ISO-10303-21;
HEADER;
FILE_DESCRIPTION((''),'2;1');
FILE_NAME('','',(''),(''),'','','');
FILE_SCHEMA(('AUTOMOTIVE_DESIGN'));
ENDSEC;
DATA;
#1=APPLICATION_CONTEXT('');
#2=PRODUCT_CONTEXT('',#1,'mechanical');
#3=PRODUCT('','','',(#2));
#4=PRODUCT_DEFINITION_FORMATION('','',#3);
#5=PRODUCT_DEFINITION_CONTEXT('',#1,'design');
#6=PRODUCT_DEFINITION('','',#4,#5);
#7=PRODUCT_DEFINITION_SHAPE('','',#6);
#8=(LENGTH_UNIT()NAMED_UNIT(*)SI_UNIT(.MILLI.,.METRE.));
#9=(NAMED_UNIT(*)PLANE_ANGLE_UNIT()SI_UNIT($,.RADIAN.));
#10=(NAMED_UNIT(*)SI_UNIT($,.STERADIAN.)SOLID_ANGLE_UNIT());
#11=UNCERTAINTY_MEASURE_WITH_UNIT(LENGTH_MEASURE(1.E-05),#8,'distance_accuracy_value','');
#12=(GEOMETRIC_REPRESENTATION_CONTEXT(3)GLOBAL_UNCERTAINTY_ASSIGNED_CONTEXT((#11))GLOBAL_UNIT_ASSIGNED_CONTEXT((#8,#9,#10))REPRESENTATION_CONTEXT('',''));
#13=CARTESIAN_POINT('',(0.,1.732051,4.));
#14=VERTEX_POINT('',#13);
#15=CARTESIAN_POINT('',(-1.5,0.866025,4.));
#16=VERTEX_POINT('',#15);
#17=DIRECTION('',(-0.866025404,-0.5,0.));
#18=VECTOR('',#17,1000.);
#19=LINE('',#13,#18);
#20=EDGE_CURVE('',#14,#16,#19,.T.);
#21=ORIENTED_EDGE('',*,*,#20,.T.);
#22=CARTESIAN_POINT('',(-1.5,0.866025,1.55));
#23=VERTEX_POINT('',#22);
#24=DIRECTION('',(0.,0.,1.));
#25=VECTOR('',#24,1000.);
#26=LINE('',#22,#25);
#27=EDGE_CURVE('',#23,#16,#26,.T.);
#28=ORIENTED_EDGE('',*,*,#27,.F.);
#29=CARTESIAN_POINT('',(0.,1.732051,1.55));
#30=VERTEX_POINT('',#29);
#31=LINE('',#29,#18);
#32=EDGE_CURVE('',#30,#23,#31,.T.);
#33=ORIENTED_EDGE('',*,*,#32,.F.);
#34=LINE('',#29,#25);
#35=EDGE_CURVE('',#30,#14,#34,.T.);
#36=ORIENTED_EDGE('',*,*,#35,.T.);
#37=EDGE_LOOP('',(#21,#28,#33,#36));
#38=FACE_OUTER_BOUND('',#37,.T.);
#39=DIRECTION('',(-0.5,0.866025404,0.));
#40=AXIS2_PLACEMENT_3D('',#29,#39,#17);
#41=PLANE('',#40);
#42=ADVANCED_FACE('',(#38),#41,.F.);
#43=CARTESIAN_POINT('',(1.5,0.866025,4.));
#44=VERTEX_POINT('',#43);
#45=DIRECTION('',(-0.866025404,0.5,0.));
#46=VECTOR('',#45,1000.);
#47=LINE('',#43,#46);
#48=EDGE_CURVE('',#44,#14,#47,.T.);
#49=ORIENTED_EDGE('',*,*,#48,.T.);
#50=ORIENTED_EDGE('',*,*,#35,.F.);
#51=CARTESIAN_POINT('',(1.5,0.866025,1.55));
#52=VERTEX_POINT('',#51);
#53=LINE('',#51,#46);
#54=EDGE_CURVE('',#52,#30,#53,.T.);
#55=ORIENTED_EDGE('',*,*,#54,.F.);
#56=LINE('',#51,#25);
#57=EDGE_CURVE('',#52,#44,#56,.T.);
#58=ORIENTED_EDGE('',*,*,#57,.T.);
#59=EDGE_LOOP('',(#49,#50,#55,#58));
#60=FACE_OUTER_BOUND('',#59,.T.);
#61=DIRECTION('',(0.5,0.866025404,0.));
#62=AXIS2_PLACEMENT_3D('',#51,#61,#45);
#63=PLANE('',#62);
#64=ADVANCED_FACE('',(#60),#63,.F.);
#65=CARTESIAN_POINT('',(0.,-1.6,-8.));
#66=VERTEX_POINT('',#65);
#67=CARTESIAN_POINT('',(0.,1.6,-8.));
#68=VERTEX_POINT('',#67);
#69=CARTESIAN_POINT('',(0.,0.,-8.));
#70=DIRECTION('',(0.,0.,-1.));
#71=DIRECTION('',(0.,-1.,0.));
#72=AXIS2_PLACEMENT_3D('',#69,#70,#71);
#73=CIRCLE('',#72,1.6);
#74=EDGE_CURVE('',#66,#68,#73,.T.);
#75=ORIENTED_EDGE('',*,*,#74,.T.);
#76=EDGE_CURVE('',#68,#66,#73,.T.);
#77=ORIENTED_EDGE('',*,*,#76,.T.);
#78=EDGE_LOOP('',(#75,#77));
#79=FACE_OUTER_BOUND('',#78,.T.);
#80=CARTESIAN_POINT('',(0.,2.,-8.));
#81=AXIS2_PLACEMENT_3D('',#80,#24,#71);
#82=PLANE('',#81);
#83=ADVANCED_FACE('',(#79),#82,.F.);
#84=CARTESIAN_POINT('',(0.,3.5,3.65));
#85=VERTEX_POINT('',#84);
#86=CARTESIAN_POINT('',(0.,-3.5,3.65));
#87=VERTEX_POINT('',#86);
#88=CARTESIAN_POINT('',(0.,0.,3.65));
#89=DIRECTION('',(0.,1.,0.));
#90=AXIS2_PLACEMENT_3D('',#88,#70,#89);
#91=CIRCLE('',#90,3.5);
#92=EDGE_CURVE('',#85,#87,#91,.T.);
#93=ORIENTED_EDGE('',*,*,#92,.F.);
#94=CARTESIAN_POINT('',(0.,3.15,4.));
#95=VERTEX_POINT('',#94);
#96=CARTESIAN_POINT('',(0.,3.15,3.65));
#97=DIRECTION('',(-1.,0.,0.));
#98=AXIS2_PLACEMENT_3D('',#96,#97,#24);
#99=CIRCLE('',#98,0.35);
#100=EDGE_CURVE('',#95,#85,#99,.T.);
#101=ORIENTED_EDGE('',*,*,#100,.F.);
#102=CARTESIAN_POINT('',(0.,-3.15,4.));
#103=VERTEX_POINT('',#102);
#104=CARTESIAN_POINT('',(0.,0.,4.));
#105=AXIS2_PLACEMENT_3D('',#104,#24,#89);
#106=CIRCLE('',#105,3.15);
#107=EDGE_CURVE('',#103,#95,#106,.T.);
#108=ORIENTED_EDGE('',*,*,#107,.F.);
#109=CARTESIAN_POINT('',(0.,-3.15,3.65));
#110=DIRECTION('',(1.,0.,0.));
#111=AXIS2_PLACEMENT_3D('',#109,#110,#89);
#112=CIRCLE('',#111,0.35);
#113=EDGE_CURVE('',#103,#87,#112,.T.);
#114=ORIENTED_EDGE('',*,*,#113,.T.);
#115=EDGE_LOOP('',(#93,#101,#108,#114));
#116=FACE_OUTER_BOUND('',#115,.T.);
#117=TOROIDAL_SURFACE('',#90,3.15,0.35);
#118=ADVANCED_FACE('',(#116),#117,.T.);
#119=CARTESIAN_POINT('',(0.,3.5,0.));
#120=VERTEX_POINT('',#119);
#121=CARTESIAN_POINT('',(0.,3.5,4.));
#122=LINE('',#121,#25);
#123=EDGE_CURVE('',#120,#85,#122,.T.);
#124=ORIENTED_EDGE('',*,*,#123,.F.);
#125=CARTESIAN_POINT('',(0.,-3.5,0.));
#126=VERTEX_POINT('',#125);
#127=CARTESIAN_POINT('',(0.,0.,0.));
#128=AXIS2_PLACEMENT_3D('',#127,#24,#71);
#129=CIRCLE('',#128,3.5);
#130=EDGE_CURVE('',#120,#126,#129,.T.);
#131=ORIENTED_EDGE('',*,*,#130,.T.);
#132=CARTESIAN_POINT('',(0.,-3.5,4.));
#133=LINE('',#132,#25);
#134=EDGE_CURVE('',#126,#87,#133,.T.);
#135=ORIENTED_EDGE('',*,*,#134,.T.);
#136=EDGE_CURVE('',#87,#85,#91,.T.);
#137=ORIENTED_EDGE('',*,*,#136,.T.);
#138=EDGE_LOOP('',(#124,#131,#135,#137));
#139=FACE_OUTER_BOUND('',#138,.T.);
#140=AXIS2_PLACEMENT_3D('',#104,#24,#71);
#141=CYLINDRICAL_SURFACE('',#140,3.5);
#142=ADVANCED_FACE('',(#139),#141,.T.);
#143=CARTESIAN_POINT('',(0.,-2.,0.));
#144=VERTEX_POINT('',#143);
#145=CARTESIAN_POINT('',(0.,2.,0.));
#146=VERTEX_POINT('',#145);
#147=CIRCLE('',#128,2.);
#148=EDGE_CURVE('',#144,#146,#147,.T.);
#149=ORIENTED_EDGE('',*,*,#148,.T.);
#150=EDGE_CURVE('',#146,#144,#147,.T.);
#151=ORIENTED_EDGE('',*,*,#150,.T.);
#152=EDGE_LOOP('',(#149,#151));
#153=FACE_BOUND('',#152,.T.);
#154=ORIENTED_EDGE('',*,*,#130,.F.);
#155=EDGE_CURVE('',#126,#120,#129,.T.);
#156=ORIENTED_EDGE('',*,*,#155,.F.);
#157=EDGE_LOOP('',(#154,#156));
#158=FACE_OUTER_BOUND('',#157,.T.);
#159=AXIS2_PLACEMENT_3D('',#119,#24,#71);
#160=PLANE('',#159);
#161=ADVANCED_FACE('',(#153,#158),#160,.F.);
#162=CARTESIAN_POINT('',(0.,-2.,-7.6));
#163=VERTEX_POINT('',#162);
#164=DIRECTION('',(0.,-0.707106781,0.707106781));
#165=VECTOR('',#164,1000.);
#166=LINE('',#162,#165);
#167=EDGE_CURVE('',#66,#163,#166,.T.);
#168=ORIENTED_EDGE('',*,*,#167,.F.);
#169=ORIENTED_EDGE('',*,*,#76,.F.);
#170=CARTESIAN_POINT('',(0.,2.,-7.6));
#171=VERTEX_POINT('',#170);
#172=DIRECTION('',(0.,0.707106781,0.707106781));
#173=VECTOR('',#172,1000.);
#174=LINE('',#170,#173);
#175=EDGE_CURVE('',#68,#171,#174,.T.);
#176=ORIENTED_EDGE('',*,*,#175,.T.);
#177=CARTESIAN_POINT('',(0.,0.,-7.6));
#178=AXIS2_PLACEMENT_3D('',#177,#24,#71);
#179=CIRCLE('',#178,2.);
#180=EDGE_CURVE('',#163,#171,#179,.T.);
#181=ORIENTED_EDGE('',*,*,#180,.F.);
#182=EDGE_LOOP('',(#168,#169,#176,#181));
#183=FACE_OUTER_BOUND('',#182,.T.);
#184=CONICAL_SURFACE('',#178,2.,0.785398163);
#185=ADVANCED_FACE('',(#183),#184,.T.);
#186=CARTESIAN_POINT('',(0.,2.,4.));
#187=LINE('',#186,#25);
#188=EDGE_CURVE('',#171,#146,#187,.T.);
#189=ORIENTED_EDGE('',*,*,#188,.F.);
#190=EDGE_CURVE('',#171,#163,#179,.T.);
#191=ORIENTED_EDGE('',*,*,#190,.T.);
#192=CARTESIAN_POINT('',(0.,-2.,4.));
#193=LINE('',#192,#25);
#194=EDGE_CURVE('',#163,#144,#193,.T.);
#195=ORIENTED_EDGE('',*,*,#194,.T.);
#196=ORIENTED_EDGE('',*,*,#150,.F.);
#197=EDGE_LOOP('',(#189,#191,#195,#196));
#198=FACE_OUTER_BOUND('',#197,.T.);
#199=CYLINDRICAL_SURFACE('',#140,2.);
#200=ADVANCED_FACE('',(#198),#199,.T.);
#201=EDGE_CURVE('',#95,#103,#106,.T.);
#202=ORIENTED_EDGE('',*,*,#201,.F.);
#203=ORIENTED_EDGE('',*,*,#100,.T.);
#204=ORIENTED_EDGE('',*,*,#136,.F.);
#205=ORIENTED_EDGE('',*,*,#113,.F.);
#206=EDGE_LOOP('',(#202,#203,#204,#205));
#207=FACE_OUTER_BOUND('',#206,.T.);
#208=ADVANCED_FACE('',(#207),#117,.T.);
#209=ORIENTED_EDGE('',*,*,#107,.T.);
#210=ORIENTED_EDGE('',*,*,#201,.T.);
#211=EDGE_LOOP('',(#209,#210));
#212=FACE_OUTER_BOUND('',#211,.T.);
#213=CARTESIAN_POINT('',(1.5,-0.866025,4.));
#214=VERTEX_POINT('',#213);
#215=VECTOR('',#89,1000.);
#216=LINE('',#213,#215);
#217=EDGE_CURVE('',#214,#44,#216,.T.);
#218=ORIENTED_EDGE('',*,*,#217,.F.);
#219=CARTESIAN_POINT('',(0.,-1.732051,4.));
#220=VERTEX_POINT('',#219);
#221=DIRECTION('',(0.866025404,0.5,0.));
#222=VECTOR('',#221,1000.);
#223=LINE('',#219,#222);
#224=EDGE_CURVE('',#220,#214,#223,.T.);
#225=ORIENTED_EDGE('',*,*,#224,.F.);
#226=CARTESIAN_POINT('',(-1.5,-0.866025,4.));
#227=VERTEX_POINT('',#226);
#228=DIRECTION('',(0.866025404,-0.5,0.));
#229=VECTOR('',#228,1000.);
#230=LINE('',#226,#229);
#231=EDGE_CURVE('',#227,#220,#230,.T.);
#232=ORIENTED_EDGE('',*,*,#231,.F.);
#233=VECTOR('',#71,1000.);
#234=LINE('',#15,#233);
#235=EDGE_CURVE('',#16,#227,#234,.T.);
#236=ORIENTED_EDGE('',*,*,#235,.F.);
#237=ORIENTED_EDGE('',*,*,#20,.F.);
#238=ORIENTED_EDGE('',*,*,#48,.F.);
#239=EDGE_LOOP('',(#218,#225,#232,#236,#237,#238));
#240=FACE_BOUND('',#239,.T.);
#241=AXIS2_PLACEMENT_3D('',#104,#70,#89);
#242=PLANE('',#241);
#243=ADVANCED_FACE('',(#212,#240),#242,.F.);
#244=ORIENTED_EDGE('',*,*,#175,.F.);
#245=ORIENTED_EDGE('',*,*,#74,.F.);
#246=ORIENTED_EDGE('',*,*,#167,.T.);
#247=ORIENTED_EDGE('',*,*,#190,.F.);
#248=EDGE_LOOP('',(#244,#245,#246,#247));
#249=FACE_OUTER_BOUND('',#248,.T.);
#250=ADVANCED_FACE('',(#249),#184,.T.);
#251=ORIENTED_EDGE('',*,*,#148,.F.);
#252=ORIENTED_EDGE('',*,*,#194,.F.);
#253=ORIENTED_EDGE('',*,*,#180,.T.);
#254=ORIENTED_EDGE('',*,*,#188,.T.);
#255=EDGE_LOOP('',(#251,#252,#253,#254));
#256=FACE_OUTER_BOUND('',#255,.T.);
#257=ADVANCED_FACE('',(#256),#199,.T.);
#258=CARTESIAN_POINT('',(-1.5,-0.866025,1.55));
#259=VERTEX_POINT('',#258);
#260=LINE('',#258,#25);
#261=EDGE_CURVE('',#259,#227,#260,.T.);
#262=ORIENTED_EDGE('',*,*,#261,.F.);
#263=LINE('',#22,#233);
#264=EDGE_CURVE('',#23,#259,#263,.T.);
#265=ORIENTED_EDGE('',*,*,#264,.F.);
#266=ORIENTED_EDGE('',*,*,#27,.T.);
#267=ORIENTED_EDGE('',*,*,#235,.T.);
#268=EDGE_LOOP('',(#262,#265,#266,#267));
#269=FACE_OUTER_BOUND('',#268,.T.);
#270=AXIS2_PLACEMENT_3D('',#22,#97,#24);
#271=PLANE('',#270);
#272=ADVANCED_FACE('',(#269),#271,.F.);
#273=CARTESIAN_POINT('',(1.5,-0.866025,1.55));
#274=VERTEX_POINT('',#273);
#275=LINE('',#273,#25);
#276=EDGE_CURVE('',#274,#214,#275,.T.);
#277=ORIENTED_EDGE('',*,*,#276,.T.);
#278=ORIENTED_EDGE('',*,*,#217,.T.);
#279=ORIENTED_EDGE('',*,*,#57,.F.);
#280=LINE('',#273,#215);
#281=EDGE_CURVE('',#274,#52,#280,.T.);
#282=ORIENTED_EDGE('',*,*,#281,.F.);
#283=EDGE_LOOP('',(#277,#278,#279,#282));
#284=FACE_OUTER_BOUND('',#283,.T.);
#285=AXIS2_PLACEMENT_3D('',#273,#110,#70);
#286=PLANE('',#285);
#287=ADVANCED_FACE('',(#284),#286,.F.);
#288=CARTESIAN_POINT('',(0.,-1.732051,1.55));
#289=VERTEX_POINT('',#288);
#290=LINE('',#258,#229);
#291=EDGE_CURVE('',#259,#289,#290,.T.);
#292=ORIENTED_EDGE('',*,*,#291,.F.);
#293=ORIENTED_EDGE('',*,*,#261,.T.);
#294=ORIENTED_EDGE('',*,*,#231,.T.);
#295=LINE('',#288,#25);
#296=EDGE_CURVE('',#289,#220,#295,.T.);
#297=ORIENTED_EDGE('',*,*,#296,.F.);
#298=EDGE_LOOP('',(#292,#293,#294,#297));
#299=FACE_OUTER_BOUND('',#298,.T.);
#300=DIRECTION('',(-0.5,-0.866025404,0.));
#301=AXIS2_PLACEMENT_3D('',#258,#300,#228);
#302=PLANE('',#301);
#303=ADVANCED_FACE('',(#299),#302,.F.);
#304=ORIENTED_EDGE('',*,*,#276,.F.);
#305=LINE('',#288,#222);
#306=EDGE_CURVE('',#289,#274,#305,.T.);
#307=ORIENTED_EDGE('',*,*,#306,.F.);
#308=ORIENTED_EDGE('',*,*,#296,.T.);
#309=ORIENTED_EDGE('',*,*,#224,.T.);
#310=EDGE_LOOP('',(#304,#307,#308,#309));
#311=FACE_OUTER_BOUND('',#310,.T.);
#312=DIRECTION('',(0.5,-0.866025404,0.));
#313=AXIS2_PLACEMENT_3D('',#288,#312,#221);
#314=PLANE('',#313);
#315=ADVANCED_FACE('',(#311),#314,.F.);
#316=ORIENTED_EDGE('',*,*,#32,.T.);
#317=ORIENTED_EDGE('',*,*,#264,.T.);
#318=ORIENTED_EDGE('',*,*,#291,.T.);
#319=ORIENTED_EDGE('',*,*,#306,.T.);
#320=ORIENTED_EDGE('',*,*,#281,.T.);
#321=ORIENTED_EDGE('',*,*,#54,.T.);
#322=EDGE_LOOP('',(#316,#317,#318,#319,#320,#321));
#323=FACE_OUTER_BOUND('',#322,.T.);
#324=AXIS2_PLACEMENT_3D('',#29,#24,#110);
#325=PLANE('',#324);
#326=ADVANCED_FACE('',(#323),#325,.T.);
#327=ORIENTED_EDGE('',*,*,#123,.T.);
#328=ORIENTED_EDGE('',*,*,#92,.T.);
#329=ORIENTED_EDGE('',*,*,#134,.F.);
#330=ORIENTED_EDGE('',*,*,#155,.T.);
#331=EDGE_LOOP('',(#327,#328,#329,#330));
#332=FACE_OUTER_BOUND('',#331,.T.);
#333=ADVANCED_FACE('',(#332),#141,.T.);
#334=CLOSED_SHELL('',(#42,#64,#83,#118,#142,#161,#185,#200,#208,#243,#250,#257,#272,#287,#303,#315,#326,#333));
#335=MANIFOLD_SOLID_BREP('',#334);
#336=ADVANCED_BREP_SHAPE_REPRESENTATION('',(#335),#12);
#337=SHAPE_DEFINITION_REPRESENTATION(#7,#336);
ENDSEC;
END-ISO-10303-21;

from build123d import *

# Parameters (mm, degrees)
CUT_EXTRUDE_1_DEPTH = 2.45
FILLET_1_R          = 0.35
CHAMFER_1_SIZE      = 0.4


with BuildPart() as part:
    # 草图3 → 旋转1 (revolve)
    with BuildSketch(Plane(origin=(0, 0, 0), x_dir=(0, 0, -1), z_dir=(1, 0, 0)), mode=Mode.PRIVATE) as revolve_1_sk:
        Polygon((-4, 0), (-4, 3.5), (0, 3.5), (0, 2), (8, 2), (8, 0), align=None)
    revolve(revolve_1_sk.sketch.rotate(Axis((0, 0, 4), (0, 0, -1)), 180), axis=Axis((0, 0, 4), (0, 0, -1)))

    # 草图4 → 切除-拉伸1 (cut)
    with BuildSketch(Plane.XY.offset(4)):
        Polygon((0, 1.732050808), (-1.5, 0.866025404), (-1.5, -0.866025404), (0, -1.732050808), (1.5, -0.866025404), (1.5, 0.866025404), align=None)
    extrude(amount=-CUT_EXTRUDE_1_DEPTH, mode=Mode.SUBTRACT)

    # 圆角1
    fillet_1_edges = [part.edges().sort_by_distance(p)[0] for p in [
        (0, 3.5, 4),
    ]]
    fillet(fillet_1_edges, radius=FILLET_1_R)

    # 倒角1
    chamfer_1_edges = [part.edges().sort_by_distance(p)[0] for p in [
        (0, 2, -8),
    ]]
    chamfer(chamfer_1_edges, length=CHAMFER_1_SIZE)


solid = part.part
